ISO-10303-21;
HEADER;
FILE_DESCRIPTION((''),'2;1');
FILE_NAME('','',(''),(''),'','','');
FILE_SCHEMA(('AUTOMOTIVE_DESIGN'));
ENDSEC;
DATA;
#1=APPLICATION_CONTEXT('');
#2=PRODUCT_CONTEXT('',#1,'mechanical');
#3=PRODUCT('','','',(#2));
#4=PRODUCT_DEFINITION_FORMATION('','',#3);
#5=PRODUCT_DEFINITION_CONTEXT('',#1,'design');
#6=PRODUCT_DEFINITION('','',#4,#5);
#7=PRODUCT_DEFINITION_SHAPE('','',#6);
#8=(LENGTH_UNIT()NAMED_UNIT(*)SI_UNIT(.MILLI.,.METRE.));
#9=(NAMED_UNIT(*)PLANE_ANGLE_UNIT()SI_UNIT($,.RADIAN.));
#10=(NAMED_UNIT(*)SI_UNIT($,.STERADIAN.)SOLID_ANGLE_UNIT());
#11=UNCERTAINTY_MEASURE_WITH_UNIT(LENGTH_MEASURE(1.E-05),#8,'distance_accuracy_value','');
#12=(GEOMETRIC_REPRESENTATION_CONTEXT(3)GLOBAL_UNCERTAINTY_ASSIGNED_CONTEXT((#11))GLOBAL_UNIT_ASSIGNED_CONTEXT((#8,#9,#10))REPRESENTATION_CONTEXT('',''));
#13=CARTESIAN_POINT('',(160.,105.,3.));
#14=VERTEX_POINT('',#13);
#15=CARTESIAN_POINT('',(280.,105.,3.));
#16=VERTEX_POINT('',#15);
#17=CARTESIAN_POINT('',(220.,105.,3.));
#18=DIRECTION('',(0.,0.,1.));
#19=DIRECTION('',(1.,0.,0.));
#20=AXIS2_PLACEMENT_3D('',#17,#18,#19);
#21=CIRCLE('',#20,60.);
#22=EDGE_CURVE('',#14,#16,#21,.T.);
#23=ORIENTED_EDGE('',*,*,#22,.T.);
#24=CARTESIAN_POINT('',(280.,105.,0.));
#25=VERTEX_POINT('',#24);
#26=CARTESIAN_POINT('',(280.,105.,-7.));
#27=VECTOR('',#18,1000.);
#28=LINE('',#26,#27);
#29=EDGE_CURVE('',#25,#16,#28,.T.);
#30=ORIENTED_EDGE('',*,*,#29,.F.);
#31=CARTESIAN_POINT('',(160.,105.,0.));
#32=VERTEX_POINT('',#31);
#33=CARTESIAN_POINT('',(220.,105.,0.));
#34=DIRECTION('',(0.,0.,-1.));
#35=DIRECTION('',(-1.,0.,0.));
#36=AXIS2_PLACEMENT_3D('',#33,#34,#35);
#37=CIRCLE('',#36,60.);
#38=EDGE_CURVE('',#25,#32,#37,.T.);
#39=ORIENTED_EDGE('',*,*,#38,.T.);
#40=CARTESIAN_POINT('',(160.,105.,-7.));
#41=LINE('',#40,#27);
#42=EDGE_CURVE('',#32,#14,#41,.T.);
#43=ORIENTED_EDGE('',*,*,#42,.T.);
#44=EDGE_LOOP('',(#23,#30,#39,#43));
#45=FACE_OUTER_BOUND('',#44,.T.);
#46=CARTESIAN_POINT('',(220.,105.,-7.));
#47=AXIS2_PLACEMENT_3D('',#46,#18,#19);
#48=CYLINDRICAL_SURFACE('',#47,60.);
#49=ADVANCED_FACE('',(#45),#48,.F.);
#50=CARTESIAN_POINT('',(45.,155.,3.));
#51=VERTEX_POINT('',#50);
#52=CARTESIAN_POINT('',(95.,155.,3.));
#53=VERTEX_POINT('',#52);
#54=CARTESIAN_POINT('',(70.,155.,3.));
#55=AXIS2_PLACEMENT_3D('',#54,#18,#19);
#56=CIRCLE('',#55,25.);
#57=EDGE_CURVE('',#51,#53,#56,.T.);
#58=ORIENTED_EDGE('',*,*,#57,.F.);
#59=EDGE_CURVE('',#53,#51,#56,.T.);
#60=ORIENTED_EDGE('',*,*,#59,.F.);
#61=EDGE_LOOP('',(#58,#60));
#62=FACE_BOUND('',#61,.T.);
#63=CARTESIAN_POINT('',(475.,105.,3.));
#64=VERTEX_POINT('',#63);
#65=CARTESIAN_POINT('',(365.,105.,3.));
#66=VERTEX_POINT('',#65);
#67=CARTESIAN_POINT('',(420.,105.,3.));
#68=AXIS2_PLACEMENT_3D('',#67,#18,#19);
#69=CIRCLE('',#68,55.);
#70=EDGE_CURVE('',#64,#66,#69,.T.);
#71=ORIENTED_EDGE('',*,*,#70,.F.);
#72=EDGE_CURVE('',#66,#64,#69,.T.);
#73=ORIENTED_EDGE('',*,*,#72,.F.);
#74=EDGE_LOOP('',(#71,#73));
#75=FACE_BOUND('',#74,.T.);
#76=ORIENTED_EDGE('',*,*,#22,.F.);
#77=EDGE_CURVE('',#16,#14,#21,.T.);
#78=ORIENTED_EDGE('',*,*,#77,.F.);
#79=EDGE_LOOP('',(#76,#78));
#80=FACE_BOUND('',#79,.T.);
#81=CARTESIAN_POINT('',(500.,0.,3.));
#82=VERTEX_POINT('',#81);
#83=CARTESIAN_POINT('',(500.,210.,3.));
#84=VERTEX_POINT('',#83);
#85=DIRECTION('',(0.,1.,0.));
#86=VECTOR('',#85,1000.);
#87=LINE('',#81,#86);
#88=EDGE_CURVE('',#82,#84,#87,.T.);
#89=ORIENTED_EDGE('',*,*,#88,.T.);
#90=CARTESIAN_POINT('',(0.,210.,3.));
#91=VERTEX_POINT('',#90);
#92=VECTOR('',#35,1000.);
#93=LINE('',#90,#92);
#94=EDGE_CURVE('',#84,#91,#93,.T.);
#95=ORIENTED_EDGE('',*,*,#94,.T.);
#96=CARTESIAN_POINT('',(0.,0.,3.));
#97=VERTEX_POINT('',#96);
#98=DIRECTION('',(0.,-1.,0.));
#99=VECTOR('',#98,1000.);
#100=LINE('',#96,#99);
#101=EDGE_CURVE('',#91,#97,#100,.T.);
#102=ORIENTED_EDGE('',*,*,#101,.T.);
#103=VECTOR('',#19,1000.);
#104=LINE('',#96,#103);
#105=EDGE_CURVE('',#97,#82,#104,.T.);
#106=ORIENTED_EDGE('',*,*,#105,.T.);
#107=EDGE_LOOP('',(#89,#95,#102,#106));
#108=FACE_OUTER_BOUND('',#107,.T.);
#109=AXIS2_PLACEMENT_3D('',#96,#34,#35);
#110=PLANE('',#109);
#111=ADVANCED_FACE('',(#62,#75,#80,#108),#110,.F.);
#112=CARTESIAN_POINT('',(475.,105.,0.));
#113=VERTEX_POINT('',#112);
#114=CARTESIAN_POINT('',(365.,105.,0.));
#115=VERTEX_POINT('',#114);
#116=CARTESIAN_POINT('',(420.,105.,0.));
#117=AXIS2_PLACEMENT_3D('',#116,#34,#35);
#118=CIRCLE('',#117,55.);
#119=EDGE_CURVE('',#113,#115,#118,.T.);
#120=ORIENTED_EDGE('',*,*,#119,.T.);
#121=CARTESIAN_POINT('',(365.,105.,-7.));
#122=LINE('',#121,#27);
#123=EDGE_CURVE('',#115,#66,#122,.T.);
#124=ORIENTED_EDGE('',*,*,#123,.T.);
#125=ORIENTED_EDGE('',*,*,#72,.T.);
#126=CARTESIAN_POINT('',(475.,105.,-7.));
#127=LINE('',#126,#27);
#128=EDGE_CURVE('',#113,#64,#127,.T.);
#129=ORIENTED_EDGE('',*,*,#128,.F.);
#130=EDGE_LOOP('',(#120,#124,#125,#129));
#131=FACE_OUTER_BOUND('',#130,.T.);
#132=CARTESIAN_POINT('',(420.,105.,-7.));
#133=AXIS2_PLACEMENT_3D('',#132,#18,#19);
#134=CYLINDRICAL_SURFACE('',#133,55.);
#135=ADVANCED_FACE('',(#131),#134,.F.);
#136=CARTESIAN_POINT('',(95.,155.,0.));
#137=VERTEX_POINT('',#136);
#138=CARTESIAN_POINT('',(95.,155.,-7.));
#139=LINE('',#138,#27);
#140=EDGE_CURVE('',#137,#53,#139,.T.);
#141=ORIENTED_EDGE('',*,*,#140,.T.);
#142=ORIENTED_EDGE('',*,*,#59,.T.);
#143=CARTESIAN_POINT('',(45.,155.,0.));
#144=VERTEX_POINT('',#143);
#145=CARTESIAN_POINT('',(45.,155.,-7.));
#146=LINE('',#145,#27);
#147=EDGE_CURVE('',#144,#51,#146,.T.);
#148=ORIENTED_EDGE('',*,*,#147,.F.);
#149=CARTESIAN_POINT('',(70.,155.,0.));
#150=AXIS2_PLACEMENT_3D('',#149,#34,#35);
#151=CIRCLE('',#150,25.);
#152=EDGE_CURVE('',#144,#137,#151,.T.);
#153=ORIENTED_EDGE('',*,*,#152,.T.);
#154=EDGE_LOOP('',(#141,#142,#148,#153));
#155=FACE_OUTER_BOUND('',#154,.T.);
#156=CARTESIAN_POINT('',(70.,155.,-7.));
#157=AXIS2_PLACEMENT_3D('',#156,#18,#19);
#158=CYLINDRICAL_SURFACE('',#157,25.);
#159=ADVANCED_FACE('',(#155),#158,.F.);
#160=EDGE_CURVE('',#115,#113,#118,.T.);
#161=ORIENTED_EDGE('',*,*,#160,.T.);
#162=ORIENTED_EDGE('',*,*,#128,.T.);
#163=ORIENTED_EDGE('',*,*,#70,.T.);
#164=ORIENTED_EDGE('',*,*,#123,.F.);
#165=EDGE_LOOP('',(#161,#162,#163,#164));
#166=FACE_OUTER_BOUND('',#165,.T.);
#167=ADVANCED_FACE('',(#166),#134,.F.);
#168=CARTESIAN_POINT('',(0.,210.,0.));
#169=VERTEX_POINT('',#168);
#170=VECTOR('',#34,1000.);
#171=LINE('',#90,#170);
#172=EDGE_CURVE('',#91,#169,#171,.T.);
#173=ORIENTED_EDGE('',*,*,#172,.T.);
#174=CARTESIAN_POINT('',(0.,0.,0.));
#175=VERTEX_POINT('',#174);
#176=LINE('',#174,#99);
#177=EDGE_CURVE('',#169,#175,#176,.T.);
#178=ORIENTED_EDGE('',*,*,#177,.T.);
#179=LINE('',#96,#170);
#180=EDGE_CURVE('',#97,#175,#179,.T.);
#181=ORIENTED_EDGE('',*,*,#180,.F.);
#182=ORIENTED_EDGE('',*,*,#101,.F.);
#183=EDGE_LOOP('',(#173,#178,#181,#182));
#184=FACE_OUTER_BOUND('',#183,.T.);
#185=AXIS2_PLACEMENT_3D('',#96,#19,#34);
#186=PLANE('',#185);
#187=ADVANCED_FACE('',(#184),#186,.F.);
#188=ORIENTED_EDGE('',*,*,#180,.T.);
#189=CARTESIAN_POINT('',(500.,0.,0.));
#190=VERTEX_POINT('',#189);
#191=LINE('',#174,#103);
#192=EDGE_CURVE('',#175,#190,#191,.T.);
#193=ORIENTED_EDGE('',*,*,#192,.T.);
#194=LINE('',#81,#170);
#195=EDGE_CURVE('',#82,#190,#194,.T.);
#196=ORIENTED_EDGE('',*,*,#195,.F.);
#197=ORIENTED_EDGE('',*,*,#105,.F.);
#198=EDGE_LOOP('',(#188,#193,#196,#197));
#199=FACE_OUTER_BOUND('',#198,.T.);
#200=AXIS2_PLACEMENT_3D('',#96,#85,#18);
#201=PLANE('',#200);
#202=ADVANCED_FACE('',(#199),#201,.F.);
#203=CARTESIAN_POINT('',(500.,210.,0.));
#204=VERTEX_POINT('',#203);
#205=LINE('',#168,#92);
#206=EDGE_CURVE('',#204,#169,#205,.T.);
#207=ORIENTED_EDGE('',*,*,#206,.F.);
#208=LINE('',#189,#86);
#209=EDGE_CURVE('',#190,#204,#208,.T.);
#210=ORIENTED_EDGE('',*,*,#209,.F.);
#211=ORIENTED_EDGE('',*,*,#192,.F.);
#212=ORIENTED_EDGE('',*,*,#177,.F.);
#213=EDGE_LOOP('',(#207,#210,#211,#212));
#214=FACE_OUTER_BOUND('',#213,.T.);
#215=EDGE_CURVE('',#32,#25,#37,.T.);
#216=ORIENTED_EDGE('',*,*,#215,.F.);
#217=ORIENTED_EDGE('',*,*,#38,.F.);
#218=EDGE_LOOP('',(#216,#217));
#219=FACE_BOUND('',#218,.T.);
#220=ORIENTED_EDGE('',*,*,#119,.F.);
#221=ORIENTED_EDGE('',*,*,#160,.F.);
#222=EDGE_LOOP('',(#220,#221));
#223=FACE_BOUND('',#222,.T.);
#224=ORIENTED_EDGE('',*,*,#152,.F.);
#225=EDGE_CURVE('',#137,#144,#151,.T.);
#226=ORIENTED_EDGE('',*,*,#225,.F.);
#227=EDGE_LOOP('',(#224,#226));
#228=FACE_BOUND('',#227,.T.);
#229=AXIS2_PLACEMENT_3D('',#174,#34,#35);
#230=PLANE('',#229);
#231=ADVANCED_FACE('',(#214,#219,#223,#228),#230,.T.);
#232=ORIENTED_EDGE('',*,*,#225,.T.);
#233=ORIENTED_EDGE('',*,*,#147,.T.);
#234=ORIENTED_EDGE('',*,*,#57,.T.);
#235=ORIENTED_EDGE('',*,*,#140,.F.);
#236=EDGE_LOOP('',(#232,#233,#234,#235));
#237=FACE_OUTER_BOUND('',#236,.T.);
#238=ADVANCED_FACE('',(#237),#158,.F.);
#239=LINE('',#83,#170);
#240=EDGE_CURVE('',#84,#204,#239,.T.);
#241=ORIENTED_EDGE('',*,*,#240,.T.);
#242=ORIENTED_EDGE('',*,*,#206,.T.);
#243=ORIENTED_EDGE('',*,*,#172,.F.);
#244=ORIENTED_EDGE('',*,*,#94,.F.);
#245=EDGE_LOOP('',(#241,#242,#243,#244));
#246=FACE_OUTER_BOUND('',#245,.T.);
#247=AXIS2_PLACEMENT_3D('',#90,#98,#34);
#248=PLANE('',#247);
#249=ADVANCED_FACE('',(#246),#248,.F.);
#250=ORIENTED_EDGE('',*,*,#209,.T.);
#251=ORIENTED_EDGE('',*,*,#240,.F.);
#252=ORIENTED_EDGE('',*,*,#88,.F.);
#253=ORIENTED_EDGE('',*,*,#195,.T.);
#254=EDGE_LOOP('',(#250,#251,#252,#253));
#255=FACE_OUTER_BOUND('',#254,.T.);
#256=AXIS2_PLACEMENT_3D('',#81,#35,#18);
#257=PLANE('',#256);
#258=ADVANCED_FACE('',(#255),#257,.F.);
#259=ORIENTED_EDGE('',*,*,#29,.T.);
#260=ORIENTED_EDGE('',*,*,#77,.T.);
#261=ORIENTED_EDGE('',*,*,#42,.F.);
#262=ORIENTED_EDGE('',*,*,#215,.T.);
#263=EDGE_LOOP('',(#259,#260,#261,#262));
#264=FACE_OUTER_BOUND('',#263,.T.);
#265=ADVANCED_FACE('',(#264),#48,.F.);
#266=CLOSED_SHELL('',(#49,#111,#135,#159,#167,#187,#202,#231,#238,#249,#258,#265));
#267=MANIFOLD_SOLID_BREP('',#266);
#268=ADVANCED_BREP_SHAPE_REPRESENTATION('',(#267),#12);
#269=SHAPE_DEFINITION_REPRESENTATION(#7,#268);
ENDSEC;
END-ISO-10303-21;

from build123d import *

# Parameters (mm, degrees)
SKETCH1_W           = 500
SKETCH1_H           = 210
BOSS_EXTRUDE1_DEPTH = 3
SKETCH2_R           = 55
SKETCH2_R_2         = 60
SKETCH2_R_3         = 25
CUT_EXTRUDE1_DEPTH  = 10


with BuildPart() as part:
    # Sketch1 → Boss-Extrude1 (new body)
    with BuildSketch(Plane.XY):
        with Locations((250, 105)):
            Rectangle(SKETCH1_W, SKETCH1_H)
    extrude(amount=BOSS_EXTRUDE1_DEPTH)

    # Sketch2 → Cut-Extrude1 (cut)
    with BuildSketch(Plane(origin=(492, 10, 3), x_dir=(1, 0, 0), z_dir=(0, 0, 1))):
        with Locations((-72, 95)):
            Circle(SKETCH2_R)
        with Locations((-272, 95)):
            Circle(SKETCH2_R_2)
        with Locations((-422, 145)):
            Circle(SKETCH2_R_3)
    extrude(amount=-CUT_EXTRUDE1_DEPTH, mode=Mode.SUBTRACT)


solid = part.part
